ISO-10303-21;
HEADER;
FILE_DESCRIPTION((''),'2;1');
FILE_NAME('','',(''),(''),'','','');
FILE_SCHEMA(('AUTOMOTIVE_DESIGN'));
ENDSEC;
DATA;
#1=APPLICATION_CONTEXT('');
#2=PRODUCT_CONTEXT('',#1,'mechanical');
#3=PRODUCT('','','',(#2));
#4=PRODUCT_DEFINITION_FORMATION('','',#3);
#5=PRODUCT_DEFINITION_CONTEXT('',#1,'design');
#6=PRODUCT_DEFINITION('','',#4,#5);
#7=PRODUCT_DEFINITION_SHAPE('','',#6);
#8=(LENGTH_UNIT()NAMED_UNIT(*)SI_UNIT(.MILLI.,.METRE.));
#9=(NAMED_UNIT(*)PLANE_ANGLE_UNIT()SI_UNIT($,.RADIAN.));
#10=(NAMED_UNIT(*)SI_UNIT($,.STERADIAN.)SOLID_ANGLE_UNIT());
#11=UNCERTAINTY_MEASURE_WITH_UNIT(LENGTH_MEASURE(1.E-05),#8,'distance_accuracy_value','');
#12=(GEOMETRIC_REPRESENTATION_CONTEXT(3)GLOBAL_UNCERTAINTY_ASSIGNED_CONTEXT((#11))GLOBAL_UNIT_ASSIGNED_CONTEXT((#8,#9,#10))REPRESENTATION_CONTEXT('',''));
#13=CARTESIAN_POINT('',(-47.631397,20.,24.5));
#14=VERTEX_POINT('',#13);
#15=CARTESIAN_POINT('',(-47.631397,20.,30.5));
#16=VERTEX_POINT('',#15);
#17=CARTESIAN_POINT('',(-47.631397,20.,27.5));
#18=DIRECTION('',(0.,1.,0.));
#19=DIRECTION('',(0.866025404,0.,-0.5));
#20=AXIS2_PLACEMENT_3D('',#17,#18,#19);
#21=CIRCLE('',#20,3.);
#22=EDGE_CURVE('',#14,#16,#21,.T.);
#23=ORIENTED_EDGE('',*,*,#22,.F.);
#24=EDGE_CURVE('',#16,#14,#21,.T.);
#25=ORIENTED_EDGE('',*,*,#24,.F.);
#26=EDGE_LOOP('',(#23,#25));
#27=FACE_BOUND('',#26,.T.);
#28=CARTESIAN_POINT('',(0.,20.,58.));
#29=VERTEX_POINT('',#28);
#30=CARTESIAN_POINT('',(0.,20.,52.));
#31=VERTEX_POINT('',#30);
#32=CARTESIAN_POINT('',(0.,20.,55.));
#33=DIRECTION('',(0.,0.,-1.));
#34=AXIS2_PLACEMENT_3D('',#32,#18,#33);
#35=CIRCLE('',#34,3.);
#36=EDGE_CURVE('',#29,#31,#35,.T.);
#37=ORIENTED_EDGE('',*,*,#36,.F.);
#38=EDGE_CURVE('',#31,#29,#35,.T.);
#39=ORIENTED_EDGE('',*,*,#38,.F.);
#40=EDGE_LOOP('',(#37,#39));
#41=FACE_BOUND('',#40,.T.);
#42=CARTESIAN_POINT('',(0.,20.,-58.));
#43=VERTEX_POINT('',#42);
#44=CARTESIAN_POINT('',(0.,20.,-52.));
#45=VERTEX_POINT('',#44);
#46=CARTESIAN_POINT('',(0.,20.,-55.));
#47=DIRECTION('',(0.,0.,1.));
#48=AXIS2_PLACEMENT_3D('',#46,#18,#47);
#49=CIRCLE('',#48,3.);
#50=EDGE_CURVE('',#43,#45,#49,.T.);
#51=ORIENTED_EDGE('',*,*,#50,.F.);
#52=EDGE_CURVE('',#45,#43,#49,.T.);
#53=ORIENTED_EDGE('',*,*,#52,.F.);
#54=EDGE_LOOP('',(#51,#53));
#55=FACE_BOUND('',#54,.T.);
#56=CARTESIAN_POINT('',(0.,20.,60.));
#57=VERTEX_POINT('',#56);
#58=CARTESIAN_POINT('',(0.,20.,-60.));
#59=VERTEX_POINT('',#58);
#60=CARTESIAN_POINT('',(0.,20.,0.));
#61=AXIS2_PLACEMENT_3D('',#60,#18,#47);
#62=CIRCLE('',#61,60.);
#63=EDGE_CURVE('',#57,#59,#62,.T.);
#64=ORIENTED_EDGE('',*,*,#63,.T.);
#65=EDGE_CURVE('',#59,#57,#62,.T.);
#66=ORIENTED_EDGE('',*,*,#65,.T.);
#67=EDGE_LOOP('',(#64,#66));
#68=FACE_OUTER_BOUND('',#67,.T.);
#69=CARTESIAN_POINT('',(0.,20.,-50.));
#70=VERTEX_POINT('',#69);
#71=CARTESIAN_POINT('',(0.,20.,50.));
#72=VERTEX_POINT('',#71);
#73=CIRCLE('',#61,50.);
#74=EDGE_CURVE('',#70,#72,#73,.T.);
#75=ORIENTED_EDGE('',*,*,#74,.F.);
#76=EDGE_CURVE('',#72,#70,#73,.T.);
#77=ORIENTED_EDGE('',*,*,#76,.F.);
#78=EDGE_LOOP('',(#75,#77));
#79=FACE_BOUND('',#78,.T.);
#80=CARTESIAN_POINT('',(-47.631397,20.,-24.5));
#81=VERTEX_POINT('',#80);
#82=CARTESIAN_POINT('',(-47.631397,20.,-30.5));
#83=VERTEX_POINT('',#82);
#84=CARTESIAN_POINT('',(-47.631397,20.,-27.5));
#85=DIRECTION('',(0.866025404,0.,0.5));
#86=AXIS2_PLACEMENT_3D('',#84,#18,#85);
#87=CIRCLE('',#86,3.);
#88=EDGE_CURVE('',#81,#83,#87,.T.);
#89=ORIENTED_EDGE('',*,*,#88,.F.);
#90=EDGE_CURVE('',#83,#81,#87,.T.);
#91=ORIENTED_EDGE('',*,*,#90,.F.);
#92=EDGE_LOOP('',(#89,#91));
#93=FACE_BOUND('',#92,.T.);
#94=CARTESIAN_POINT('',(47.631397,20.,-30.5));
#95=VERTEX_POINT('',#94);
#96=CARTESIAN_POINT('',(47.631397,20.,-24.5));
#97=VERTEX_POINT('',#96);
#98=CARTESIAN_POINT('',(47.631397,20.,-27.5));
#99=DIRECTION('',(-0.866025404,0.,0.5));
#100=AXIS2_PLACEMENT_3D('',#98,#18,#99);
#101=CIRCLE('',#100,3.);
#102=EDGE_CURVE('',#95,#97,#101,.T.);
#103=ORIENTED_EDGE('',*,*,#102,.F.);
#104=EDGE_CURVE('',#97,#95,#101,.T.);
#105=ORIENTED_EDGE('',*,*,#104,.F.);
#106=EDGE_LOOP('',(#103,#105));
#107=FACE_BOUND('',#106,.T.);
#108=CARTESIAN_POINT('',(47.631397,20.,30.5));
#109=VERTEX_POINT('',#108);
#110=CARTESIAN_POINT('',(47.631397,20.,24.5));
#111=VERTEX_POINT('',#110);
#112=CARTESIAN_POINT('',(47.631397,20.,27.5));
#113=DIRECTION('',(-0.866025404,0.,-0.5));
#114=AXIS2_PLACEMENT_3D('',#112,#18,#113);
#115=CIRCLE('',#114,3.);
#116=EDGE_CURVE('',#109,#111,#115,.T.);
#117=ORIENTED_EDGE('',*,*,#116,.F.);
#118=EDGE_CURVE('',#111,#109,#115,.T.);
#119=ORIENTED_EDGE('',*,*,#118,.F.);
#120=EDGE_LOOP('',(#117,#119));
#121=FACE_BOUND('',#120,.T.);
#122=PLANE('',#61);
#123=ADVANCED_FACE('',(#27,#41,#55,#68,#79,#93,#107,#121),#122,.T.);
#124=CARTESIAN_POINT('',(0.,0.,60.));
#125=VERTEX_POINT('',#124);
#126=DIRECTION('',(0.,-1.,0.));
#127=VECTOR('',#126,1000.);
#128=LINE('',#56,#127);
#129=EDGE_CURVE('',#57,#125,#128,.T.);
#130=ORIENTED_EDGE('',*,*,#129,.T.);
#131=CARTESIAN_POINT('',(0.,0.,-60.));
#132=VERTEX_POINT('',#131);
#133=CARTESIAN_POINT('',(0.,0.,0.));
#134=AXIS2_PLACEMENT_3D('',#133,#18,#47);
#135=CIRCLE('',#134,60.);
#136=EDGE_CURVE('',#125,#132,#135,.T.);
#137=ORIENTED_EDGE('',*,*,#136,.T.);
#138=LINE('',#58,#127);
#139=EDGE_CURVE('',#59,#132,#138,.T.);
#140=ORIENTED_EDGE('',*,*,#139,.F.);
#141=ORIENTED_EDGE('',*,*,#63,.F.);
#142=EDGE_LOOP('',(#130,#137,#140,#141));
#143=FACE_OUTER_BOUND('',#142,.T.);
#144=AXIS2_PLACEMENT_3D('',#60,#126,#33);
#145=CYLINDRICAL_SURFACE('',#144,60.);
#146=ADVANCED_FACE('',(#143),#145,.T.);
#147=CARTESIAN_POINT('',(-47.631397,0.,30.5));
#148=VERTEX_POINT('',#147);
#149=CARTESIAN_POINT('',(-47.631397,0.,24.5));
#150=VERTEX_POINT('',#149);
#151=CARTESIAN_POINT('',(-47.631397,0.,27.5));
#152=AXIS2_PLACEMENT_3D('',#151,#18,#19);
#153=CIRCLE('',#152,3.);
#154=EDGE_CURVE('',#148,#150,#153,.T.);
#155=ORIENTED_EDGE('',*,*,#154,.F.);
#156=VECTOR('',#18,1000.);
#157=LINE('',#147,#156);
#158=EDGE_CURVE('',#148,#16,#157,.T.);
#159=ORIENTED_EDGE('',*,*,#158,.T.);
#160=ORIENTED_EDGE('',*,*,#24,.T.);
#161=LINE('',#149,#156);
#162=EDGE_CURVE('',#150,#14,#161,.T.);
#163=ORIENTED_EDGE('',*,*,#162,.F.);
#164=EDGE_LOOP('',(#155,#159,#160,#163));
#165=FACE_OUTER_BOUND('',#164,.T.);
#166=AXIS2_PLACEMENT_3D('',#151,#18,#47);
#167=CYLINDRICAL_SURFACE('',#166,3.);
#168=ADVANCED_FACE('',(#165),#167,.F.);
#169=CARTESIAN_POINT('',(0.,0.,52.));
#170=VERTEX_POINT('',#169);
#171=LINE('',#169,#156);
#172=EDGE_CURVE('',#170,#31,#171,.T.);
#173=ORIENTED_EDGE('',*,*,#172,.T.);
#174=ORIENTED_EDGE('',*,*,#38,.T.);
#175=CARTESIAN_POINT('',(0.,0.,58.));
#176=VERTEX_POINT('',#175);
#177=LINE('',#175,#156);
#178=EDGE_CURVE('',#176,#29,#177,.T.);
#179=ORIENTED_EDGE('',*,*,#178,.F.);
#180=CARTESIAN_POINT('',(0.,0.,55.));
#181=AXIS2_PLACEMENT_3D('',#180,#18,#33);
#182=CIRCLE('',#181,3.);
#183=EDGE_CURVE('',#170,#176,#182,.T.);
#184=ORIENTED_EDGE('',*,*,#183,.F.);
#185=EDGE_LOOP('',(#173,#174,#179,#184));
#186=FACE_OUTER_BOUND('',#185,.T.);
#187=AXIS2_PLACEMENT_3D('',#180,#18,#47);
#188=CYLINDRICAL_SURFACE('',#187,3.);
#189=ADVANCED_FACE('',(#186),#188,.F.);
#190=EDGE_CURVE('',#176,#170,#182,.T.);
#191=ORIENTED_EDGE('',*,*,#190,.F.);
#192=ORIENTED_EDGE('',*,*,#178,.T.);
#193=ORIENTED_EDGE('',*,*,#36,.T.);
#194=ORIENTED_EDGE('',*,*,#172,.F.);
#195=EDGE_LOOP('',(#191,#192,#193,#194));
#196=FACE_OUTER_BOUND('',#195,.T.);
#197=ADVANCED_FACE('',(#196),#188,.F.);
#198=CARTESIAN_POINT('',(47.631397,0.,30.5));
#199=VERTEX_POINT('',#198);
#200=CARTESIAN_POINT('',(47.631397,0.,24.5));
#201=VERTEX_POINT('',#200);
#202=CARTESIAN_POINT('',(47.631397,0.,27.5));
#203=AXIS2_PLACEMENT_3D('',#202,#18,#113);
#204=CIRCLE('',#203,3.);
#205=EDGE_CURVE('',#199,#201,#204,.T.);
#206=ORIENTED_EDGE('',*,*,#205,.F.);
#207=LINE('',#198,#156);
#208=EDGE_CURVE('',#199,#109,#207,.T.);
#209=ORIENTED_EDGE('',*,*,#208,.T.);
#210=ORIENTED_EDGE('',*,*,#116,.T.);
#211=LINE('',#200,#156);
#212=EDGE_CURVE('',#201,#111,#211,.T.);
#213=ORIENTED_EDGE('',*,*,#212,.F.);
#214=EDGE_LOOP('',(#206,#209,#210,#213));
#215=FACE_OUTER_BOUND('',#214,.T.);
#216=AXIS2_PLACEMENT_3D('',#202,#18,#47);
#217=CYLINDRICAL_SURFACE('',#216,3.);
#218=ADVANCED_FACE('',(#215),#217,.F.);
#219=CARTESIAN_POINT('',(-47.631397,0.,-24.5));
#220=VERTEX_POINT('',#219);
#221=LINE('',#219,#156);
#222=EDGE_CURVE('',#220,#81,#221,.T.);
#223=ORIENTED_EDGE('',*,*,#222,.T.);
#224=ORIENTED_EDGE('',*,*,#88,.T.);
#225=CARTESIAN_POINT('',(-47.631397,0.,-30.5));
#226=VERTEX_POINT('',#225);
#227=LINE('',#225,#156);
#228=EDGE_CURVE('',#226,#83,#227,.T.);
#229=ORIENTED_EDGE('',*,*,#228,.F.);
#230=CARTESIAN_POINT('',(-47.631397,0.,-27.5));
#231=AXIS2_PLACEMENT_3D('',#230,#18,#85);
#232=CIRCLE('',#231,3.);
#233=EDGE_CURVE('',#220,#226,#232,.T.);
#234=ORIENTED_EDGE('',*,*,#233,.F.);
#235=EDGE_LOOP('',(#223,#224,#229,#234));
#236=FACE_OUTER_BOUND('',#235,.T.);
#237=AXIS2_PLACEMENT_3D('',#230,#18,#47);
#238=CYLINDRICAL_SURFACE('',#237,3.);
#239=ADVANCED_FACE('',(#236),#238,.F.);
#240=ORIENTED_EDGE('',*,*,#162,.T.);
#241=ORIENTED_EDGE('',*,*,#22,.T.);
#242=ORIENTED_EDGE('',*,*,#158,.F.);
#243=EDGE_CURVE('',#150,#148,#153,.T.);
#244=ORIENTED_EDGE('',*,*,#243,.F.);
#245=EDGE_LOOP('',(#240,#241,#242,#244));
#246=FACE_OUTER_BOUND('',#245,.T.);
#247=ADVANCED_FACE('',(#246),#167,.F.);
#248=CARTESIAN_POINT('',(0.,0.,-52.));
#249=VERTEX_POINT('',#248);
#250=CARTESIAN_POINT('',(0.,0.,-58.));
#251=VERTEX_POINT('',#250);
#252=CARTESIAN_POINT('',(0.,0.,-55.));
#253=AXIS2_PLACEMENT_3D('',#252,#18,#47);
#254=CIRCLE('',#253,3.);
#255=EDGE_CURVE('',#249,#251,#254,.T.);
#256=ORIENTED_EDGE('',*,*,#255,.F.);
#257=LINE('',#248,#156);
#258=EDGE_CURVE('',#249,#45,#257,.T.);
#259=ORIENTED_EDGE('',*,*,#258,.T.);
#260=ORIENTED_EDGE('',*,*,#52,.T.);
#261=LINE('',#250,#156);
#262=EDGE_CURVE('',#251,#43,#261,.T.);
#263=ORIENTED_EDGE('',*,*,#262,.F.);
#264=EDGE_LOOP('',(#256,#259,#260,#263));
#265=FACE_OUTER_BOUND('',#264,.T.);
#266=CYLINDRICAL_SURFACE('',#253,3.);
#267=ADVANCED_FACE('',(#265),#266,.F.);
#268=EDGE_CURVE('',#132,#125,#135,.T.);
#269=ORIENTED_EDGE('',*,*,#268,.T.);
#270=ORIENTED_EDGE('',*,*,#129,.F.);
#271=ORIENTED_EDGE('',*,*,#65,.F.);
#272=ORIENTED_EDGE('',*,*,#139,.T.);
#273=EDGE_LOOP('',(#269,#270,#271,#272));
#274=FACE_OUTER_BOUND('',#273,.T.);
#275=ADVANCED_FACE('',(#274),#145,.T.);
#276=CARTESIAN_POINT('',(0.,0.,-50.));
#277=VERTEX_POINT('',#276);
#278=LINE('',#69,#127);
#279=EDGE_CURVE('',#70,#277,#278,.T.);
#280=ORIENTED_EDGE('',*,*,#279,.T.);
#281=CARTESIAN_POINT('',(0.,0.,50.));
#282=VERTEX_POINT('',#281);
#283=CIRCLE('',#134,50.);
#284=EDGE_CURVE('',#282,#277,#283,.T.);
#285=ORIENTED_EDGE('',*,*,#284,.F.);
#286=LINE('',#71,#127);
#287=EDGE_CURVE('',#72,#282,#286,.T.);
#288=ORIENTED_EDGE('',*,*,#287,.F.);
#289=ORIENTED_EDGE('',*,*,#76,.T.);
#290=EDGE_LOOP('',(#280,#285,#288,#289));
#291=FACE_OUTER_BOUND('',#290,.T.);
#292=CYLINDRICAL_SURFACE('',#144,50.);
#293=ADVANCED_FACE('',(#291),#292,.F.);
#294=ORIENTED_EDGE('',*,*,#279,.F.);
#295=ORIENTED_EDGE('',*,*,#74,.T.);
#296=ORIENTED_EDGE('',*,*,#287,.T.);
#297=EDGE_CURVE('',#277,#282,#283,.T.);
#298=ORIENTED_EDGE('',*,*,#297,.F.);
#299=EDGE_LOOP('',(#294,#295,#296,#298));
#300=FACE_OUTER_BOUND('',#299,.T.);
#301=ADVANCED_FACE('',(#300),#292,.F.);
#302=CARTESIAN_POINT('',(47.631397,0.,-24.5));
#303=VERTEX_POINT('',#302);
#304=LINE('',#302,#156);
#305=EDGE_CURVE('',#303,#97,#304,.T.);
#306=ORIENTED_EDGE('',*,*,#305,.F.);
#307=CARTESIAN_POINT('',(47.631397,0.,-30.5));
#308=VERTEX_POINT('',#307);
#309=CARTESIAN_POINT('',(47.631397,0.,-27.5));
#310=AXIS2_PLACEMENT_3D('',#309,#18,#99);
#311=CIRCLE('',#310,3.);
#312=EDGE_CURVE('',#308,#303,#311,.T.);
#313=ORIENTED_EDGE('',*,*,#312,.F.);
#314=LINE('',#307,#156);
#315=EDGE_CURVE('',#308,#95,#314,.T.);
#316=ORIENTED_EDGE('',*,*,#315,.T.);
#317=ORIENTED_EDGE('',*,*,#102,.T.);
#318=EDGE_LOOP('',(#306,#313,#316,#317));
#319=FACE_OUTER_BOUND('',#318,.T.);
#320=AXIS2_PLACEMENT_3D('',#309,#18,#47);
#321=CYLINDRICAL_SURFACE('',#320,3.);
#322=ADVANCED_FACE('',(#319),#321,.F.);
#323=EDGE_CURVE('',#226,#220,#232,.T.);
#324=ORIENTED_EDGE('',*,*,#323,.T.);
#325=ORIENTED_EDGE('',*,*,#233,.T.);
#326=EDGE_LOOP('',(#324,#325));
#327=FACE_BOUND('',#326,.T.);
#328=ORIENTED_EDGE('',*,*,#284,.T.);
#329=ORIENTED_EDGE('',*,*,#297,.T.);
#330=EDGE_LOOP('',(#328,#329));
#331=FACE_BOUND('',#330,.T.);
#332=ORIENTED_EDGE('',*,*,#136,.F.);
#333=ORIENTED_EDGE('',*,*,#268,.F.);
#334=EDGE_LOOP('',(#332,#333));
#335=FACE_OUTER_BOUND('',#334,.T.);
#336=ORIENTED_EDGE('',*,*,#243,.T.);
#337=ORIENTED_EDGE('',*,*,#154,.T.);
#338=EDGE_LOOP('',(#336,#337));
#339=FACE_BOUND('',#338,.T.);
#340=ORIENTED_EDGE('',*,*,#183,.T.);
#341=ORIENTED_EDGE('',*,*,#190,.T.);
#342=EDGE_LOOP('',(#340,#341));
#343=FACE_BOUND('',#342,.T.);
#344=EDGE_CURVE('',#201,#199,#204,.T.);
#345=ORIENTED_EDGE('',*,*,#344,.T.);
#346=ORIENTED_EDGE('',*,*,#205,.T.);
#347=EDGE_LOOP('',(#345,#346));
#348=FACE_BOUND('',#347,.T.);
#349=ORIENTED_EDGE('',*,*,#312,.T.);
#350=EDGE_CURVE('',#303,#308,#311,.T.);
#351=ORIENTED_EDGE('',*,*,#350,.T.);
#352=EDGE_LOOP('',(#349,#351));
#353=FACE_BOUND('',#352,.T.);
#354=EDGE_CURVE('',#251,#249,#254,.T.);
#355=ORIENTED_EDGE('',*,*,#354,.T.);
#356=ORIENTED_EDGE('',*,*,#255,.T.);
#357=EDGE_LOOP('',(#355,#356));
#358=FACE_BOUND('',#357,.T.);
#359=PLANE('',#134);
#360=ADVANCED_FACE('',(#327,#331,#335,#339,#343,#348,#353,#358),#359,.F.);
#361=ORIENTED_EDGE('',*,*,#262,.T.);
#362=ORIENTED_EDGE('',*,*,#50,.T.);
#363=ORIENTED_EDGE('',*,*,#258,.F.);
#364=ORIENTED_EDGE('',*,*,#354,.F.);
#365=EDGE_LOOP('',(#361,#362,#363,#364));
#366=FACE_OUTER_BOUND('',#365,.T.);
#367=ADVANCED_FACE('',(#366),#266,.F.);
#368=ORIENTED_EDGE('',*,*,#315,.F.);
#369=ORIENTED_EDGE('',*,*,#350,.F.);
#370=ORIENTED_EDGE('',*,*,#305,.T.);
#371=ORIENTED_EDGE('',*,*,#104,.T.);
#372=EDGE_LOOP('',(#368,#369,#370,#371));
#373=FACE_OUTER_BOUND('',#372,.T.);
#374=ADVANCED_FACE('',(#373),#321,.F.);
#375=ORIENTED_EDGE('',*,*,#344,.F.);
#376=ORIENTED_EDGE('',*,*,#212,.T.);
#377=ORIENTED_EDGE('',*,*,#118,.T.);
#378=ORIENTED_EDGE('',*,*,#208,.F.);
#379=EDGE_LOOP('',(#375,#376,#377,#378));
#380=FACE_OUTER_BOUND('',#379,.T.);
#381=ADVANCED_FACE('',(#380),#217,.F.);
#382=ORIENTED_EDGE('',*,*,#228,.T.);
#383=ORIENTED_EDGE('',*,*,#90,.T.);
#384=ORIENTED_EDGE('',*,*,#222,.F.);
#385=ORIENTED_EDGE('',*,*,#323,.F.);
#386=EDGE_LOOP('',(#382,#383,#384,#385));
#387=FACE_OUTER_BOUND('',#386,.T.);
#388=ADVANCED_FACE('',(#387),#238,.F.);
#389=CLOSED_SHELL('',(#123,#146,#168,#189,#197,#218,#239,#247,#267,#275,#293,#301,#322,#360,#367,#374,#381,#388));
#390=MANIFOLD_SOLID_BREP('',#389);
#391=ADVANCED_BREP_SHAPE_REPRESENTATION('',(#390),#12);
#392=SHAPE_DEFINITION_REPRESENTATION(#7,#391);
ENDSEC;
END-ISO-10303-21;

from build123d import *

# Parameters (mm, degrees)
SKETCH_1_R               = 60
SKETCH_1_R_2             = 50
EXTRUDE_1_DEPTH          = 20
SKETCH_2_R               = 3
CUT_EXTRUDE_1_DEPTH      = 88.177978871
PATTERN_CIRCULAR_1_COUNT = 6


with BuildPart() as part:
    # 草图1 → 凸台-拉伸1 (new body)
    with BuildSketch(Plane(origin=(0, 0, 0), x_dir=(1, 0, 0), z_dir=(0, 1, 0))):
        with Locations(Location((0, 0, 0), (0, 0, 270))):
            Circle(SKETCH_1_R)
        with Locations(Location((0, 0, 0), (0, 0, 270))):
            Circle(SKETCH_1_R_2, mode=Mode.SUBTRACT)
    extrude(amount=EXTRUDE_1_DEPTH)

    # 草图2 → 切除-拉伸1 (cut, through all)
    with BuildSketch(Plane(origin=(0, 20, 0), x_dir=(1, 0, 0), z_dir=(0, 1, 0))):
        with Locations(Location((0, 55, 0), (0, 0, 270))):
            Circle(SKETCH_2_R)
    cut_extrude_1 = extrude(amount=-CUT_EXTRUDE_1_DEPTH, mode=Mode.SUBTRACT)

    # 阵列(圆周)1: 切除-拉伸1 ×6 about axis
    pattern_circular_1_axis = Axis((0, 0, 0), (0, 1, 0))
    for i in range(1, PATTERN_CIRCULAR_1_COUNT):
        add(cut_extrude_1.rotate(pattern_circular_1_axis, i * 360 / PATTERN_CIRCULAR_1_COUNT), mode=Mode.SUBTRACT)


solid = part.part
